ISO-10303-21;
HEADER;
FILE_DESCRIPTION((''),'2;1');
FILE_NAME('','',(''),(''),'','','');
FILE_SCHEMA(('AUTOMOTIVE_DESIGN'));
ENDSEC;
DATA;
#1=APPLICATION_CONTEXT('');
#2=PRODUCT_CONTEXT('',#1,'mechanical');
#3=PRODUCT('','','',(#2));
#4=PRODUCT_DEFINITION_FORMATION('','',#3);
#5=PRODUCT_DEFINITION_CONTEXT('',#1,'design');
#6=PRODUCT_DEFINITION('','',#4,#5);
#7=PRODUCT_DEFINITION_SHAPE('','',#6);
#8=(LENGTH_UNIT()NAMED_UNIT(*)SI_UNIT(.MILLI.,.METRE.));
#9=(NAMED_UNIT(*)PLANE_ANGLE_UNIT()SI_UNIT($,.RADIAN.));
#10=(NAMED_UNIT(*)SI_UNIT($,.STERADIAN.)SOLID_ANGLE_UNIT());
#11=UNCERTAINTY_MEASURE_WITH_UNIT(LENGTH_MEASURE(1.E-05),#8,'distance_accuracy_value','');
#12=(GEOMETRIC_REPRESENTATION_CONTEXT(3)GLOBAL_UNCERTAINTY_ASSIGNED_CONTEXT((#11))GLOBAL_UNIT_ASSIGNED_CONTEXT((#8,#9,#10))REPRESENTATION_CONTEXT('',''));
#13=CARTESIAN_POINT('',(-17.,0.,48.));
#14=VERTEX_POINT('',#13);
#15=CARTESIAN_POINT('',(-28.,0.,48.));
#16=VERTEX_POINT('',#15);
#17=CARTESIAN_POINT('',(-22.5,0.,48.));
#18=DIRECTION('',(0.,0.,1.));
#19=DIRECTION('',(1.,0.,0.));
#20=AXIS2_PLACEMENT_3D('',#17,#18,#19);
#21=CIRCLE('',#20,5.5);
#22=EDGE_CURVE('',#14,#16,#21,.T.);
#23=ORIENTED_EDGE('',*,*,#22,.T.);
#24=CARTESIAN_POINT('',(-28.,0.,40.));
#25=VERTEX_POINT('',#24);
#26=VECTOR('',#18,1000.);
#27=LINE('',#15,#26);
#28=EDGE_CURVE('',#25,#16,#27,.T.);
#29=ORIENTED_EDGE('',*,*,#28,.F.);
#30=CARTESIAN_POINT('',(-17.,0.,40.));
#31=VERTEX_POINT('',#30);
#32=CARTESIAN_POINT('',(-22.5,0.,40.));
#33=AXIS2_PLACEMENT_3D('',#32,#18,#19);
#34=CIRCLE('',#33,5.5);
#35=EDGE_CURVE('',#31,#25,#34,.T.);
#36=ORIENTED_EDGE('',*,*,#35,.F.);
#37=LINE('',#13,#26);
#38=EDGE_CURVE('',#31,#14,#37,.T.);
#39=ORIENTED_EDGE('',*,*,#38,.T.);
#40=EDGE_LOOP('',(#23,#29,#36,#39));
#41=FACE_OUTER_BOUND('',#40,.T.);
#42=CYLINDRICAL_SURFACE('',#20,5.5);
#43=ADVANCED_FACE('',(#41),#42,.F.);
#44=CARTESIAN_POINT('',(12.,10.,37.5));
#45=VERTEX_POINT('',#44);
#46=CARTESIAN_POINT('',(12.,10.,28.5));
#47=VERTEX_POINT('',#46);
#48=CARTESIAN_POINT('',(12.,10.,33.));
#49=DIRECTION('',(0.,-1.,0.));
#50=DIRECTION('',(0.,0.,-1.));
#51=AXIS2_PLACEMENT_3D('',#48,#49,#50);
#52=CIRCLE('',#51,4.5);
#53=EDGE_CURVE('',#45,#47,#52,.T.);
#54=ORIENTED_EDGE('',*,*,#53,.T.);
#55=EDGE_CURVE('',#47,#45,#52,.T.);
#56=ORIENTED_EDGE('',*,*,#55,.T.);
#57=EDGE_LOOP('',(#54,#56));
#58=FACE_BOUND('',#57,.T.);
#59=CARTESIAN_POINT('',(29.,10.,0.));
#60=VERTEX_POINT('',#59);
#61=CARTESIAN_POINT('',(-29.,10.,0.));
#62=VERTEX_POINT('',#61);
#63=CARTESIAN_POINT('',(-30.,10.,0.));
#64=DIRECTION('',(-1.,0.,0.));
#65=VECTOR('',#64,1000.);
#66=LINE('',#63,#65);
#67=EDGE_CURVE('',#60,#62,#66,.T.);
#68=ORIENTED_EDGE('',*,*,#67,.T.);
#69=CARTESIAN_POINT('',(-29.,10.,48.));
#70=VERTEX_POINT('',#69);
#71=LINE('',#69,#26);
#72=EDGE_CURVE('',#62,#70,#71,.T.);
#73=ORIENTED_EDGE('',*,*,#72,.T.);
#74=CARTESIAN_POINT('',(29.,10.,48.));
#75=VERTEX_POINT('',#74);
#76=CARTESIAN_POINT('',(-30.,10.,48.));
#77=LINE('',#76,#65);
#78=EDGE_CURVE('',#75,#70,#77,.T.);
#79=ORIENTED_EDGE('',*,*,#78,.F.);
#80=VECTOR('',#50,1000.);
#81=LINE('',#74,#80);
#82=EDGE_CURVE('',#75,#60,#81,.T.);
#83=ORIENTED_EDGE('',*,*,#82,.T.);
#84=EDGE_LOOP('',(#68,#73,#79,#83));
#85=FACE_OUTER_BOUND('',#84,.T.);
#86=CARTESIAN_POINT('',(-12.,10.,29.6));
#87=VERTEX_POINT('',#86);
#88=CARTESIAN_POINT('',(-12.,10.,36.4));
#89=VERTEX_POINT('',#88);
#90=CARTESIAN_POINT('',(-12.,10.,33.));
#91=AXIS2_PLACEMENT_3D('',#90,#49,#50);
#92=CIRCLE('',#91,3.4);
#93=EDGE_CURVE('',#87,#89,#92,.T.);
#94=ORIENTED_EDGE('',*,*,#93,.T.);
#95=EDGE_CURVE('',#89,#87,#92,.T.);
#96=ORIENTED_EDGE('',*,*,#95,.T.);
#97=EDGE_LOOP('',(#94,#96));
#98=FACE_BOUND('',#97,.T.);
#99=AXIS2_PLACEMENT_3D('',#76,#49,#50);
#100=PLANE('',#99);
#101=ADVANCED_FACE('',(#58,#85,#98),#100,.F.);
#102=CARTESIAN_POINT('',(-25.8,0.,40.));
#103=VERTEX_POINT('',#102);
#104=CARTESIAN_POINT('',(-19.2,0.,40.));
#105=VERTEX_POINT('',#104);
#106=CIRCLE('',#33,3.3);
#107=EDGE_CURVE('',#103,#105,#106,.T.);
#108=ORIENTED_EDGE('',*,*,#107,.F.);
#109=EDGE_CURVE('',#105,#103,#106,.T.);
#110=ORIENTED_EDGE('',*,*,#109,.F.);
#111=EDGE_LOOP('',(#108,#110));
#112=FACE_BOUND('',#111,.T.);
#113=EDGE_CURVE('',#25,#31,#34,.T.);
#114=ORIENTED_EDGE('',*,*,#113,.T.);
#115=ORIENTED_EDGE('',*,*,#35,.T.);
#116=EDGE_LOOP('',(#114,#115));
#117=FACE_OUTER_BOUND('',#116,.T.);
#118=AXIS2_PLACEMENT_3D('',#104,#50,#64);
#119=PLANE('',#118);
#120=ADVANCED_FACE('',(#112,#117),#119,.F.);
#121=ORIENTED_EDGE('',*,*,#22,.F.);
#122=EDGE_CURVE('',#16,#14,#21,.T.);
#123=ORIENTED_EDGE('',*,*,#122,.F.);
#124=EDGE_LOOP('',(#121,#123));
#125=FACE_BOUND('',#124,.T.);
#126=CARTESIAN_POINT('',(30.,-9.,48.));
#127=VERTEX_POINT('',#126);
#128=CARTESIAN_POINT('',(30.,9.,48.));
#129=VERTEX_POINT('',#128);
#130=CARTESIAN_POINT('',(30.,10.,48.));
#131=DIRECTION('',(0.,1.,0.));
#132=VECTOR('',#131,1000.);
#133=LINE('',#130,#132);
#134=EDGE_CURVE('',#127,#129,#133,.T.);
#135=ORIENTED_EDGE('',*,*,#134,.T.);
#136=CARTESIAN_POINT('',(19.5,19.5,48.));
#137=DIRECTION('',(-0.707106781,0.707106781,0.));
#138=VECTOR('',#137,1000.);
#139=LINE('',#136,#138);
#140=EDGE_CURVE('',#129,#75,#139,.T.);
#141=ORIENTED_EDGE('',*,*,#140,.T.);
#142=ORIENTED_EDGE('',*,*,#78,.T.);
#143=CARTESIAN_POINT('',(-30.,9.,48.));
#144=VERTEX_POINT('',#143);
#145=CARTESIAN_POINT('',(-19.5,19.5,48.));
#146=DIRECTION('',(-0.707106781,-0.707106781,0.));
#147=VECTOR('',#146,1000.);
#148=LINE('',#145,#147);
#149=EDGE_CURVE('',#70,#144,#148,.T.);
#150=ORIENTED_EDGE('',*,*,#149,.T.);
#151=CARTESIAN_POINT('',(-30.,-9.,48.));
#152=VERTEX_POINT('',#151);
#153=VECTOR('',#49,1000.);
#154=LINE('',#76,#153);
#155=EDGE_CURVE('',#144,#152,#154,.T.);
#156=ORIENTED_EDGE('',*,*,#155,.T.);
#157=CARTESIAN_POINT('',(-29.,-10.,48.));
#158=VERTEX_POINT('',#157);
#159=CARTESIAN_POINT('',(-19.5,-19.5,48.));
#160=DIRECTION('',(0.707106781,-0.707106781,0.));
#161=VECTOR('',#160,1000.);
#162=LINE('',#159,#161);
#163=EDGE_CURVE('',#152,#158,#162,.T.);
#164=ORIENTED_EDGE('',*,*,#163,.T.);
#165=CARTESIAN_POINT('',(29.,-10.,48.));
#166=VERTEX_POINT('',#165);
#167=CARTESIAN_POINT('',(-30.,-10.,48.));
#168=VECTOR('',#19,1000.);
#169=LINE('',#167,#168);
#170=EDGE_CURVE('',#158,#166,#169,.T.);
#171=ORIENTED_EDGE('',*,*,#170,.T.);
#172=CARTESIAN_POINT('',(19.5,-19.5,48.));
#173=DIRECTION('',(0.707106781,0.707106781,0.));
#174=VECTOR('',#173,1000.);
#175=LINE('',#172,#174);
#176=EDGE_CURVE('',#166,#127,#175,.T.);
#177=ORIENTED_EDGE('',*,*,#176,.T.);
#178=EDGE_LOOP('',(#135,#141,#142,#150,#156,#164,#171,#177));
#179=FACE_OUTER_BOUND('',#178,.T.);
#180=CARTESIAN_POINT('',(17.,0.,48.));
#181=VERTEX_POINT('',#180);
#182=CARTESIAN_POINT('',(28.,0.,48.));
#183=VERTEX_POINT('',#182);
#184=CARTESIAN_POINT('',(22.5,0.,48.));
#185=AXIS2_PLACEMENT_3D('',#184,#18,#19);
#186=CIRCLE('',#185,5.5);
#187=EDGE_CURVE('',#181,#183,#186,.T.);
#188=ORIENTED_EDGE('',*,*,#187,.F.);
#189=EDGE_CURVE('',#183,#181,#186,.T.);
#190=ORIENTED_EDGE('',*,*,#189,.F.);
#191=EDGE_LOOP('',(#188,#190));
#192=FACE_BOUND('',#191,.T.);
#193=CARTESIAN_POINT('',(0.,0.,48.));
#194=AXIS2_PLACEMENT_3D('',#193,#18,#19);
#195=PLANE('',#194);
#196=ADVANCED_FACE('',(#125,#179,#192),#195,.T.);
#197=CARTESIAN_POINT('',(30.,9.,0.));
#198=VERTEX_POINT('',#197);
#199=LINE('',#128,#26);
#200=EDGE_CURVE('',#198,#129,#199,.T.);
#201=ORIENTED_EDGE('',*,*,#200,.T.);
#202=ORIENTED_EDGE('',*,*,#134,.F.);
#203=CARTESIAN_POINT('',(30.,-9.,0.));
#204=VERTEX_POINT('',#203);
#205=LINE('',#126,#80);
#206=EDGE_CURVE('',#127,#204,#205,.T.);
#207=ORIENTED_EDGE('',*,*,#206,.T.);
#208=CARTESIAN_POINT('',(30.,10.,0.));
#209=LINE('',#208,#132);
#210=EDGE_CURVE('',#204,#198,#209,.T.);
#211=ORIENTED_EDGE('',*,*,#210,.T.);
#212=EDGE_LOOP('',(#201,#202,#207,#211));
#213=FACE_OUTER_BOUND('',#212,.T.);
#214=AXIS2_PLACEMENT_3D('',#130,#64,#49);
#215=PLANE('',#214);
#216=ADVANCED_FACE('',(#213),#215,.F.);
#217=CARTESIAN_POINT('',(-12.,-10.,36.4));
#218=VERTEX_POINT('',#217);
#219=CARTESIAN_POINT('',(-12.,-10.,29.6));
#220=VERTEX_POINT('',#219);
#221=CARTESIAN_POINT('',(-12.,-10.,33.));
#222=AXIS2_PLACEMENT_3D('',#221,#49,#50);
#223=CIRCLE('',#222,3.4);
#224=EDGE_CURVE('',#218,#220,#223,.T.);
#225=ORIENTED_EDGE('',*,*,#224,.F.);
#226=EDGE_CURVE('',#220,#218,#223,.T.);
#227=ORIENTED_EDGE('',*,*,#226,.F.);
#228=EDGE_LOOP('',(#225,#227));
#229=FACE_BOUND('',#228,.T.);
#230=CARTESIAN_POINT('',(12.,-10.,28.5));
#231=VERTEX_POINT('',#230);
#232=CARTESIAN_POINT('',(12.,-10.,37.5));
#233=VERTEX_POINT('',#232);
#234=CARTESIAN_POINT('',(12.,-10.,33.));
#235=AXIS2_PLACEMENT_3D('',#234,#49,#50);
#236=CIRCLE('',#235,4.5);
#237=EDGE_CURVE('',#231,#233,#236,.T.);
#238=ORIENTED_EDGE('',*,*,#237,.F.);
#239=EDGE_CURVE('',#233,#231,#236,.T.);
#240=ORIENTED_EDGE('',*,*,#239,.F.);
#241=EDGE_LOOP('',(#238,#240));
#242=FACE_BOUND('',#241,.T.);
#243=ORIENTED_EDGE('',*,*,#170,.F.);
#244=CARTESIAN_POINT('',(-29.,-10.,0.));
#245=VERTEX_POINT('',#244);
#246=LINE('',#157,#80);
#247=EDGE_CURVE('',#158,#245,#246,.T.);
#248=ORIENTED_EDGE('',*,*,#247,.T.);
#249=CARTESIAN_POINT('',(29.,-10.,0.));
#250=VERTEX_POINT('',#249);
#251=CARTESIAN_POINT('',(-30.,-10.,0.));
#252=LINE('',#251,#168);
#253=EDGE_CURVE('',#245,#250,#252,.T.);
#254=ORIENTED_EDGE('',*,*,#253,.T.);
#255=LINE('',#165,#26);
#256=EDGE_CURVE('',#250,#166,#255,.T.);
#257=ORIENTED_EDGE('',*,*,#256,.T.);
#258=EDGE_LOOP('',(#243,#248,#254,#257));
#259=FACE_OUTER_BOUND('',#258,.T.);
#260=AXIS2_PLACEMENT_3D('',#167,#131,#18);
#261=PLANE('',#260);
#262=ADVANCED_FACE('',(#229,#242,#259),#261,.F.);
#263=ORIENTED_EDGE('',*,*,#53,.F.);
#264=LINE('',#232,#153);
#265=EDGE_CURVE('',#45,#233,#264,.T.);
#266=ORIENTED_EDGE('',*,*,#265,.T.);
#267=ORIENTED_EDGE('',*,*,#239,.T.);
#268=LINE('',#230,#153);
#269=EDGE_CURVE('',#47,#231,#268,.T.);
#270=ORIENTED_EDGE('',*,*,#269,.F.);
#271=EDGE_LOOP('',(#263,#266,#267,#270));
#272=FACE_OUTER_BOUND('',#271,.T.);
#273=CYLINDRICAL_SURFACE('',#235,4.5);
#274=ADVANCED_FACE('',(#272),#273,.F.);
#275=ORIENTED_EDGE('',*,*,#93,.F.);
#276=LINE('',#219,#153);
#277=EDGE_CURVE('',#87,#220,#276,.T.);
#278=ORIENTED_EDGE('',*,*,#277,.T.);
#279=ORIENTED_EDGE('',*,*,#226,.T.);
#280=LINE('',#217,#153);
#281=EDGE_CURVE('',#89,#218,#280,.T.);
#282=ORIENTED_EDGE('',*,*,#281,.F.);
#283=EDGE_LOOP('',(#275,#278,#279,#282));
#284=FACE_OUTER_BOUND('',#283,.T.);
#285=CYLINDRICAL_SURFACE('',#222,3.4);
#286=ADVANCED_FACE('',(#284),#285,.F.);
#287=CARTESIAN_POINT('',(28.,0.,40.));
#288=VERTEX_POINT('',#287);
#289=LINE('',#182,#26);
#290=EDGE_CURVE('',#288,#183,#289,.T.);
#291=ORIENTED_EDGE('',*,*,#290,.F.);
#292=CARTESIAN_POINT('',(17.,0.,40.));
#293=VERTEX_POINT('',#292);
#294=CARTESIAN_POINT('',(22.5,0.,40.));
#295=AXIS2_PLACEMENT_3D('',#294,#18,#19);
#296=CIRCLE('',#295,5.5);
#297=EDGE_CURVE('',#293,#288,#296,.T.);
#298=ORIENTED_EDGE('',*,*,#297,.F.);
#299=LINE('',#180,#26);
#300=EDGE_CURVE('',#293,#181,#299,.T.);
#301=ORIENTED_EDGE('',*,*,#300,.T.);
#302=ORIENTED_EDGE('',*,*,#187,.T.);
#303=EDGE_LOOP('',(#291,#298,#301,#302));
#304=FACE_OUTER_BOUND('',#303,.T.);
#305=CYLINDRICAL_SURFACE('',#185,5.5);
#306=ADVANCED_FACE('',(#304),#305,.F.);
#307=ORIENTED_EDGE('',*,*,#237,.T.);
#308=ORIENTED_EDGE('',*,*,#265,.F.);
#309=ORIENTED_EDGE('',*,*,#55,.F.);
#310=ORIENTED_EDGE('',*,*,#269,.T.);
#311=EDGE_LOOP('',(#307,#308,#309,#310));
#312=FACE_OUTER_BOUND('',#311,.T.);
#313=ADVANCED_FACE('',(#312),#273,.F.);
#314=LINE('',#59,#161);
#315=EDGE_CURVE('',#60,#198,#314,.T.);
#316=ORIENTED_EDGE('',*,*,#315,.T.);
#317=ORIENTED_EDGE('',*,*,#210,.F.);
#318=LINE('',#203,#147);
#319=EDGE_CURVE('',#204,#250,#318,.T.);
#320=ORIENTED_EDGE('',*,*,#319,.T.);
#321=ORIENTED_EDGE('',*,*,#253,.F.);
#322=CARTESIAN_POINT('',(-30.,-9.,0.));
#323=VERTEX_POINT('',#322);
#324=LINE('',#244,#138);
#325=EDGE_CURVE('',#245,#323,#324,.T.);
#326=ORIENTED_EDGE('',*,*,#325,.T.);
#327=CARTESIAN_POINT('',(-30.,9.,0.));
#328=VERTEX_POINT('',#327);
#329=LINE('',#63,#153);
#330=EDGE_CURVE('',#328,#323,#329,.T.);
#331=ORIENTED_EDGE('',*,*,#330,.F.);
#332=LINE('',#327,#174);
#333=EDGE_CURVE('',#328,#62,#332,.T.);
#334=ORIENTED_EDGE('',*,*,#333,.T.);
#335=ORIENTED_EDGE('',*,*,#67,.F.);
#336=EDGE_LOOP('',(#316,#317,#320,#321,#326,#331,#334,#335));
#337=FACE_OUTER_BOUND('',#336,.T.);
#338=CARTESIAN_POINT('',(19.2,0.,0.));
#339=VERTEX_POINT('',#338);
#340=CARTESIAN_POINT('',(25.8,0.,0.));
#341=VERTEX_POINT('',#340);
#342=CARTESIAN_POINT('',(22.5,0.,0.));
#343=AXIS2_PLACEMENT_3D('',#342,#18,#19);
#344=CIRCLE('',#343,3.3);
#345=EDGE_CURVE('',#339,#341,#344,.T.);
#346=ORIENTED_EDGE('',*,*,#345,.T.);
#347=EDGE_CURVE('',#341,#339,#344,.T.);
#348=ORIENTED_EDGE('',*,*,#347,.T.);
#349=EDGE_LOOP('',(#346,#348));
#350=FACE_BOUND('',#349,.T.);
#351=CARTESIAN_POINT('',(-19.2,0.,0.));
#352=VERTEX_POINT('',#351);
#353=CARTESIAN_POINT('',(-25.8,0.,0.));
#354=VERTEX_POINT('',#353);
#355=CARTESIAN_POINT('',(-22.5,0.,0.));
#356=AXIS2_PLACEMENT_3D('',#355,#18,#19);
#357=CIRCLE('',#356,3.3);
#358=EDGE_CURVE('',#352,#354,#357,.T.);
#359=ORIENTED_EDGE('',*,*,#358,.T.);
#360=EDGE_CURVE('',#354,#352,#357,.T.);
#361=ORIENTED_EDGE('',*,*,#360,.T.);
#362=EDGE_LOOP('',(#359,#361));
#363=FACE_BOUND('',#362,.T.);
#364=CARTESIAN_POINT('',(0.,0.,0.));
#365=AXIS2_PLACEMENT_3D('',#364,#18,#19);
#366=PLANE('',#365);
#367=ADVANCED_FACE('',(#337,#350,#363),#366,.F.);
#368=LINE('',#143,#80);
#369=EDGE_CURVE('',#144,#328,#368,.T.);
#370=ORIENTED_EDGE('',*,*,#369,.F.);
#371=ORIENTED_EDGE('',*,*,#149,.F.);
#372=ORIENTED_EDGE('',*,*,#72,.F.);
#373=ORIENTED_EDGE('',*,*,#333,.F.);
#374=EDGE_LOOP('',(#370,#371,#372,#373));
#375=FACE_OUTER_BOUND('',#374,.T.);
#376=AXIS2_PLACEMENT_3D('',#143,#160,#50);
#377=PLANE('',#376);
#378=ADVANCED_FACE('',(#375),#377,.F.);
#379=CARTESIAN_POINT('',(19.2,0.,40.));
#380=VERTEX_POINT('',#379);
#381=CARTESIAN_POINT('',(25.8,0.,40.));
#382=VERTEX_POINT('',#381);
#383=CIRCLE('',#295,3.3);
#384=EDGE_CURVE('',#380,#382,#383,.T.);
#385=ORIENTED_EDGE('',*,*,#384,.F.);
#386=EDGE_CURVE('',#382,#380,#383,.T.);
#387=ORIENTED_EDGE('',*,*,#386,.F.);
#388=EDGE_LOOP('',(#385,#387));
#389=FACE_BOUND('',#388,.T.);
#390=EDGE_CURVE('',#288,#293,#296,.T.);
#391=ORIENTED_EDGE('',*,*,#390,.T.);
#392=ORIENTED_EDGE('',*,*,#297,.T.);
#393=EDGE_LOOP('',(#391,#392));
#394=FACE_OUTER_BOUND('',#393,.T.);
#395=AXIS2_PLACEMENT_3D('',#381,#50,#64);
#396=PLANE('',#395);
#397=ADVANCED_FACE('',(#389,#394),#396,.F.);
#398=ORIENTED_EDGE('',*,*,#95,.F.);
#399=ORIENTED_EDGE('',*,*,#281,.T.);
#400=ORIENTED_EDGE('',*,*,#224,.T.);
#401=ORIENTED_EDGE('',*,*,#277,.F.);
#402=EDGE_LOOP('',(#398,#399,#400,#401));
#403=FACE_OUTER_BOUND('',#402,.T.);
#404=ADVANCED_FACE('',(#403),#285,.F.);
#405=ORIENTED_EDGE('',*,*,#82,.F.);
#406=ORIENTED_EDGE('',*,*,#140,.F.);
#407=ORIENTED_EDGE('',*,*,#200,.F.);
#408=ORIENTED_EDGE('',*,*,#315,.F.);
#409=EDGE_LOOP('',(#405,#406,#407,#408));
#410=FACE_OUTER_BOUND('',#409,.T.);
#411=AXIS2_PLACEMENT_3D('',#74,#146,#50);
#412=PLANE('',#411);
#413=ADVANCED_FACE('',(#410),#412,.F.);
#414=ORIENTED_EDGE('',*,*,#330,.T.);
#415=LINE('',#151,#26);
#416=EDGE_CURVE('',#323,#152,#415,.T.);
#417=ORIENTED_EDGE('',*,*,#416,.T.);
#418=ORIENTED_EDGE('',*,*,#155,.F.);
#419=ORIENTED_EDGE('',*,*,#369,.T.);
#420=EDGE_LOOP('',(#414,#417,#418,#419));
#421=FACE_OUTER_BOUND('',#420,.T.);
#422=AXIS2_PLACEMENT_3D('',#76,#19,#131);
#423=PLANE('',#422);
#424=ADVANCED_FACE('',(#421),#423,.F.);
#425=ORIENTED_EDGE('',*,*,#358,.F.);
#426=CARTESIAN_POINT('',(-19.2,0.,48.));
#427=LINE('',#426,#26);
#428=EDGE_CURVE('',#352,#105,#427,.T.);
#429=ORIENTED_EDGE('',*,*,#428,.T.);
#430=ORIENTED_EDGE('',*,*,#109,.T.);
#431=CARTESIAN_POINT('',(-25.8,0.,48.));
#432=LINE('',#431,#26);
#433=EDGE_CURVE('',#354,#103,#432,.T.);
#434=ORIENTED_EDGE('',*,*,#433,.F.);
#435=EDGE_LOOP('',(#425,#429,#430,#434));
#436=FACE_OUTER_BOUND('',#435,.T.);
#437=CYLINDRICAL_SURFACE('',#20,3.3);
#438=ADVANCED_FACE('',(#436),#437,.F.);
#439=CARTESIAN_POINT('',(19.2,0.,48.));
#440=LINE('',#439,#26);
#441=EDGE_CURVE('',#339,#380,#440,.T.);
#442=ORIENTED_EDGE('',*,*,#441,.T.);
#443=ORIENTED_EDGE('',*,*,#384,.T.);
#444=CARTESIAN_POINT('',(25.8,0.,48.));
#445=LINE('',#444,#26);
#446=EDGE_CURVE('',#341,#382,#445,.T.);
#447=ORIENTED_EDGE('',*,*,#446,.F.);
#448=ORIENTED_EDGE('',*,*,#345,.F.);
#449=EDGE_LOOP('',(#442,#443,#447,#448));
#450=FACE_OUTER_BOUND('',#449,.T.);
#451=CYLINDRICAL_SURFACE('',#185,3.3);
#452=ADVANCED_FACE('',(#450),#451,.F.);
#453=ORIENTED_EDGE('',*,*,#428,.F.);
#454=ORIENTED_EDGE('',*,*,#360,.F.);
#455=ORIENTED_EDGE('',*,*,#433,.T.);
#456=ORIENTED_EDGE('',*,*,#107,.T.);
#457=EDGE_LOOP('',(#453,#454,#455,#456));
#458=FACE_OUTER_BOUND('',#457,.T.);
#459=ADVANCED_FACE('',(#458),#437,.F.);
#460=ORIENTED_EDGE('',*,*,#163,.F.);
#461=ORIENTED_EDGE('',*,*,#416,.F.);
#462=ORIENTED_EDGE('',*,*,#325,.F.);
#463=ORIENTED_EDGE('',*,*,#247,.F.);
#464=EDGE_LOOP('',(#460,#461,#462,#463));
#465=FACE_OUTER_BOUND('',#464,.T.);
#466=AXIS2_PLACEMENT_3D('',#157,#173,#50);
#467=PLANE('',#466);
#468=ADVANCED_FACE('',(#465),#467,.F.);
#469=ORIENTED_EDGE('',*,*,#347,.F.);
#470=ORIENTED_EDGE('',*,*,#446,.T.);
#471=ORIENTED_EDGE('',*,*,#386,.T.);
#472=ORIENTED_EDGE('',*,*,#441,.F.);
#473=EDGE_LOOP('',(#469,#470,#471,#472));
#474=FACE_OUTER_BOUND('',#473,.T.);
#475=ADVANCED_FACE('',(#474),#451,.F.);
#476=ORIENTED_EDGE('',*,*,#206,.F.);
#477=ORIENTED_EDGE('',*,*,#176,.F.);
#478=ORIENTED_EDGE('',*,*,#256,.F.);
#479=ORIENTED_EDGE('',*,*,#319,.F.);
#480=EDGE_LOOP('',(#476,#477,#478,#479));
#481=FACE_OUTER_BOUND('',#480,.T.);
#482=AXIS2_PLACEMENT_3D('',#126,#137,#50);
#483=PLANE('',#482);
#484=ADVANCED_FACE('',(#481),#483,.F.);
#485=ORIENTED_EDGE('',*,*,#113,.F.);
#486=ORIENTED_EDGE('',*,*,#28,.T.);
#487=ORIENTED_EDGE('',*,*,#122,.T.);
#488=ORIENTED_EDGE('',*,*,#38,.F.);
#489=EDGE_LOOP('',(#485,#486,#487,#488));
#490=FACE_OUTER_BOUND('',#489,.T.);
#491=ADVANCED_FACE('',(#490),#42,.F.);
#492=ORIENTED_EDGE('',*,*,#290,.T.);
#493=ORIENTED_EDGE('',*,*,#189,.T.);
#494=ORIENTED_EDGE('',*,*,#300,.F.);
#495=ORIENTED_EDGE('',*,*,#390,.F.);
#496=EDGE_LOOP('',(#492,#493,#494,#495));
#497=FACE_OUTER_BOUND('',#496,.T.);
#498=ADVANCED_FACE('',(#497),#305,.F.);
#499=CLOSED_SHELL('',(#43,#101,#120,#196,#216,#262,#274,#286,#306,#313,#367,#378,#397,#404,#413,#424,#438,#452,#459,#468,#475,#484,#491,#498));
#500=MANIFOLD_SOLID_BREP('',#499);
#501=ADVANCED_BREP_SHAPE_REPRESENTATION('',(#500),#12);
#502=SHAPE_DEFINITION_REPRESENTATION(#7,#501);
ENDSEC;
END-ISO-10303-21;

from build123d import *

# Parameters (mm, degrees)
SKETCH1_W                                           = 60
SKETCH1_H                                           = 20
BOSS_EXTRUDE1_DEPTH                                 = 48
CBORE_FOR_M6_HEX_SOCKET_HEAD_CAP_SCREW1_D           = 6.6
CBORE_FOR_M6_HEX_SOCKET_HEAD_CAP_SCREW1_CBORE_D     = 11
CBORE_FOR_M6_HEX_SOCKET_HEAD_CAP_SCREW1_CBORE_DEPTH = 8
M8_TAPPED_HOLE1_D                                   = 6.8
M10X1_0_TAPPED_HOLE1_D                              = 9
CHAMFER1_SIZE                                       = 1


with BuildPart() as part:
    # Sketch1 → Boss-Extrude1 (new body)
    with BuildSketch(Plane.XY):
        Rectangle(SKETCH1_W, SKETCH1_H)
    extrude(amount=BOSS_EXTRUDE1_DEPTH)

    # CBORE for M6 Hex Socket Head Cap Screw1 (through all)
    with Locations(Plane.XY.offset(48)):
        with Locations((-22.5, 0), (22.5, 0)):
            CounterBoreHole(CBORE_FOR_M6_HEX_SOCKET_HEAD_CAP_SCREW1_D / 2, CBORE_FOR_M6_HEX_SOCKET_HEAD_CAP_SCREW1_CBORE_D / 2, CBORE_FOR_M6_HEX_SOCKET_HEAD_CAP_SCREW1_CBORE_DEPTH)

    # M8 Tapped Hole1 (through all)
    with Locations(Plane.XZ.offset(10)):
        with Locations((-12, 33)):
            Hole(M8_TAPPED_HOLE1_D / 2)

    # M10x1.0 Tapped Hole1 (through all)
    with Locations(Plane.XZ.offset(10)):
        with Locations((12, 33)):
            Hole(M10X1_0_TAPPED_HOLE1_D / 2)

    # Chamfer1
    chamfer1_edges = [part.edges().sort_by_distance(p)[0] for p in [
        (30, -10, 24),
        (-30, -10, 24),
        (-30, 10, 24),
        (30, 10, 24),
    ]]
    chamfer(chamfer1_edges, length=CHAMFER1_SIZE)


solid = part.part
